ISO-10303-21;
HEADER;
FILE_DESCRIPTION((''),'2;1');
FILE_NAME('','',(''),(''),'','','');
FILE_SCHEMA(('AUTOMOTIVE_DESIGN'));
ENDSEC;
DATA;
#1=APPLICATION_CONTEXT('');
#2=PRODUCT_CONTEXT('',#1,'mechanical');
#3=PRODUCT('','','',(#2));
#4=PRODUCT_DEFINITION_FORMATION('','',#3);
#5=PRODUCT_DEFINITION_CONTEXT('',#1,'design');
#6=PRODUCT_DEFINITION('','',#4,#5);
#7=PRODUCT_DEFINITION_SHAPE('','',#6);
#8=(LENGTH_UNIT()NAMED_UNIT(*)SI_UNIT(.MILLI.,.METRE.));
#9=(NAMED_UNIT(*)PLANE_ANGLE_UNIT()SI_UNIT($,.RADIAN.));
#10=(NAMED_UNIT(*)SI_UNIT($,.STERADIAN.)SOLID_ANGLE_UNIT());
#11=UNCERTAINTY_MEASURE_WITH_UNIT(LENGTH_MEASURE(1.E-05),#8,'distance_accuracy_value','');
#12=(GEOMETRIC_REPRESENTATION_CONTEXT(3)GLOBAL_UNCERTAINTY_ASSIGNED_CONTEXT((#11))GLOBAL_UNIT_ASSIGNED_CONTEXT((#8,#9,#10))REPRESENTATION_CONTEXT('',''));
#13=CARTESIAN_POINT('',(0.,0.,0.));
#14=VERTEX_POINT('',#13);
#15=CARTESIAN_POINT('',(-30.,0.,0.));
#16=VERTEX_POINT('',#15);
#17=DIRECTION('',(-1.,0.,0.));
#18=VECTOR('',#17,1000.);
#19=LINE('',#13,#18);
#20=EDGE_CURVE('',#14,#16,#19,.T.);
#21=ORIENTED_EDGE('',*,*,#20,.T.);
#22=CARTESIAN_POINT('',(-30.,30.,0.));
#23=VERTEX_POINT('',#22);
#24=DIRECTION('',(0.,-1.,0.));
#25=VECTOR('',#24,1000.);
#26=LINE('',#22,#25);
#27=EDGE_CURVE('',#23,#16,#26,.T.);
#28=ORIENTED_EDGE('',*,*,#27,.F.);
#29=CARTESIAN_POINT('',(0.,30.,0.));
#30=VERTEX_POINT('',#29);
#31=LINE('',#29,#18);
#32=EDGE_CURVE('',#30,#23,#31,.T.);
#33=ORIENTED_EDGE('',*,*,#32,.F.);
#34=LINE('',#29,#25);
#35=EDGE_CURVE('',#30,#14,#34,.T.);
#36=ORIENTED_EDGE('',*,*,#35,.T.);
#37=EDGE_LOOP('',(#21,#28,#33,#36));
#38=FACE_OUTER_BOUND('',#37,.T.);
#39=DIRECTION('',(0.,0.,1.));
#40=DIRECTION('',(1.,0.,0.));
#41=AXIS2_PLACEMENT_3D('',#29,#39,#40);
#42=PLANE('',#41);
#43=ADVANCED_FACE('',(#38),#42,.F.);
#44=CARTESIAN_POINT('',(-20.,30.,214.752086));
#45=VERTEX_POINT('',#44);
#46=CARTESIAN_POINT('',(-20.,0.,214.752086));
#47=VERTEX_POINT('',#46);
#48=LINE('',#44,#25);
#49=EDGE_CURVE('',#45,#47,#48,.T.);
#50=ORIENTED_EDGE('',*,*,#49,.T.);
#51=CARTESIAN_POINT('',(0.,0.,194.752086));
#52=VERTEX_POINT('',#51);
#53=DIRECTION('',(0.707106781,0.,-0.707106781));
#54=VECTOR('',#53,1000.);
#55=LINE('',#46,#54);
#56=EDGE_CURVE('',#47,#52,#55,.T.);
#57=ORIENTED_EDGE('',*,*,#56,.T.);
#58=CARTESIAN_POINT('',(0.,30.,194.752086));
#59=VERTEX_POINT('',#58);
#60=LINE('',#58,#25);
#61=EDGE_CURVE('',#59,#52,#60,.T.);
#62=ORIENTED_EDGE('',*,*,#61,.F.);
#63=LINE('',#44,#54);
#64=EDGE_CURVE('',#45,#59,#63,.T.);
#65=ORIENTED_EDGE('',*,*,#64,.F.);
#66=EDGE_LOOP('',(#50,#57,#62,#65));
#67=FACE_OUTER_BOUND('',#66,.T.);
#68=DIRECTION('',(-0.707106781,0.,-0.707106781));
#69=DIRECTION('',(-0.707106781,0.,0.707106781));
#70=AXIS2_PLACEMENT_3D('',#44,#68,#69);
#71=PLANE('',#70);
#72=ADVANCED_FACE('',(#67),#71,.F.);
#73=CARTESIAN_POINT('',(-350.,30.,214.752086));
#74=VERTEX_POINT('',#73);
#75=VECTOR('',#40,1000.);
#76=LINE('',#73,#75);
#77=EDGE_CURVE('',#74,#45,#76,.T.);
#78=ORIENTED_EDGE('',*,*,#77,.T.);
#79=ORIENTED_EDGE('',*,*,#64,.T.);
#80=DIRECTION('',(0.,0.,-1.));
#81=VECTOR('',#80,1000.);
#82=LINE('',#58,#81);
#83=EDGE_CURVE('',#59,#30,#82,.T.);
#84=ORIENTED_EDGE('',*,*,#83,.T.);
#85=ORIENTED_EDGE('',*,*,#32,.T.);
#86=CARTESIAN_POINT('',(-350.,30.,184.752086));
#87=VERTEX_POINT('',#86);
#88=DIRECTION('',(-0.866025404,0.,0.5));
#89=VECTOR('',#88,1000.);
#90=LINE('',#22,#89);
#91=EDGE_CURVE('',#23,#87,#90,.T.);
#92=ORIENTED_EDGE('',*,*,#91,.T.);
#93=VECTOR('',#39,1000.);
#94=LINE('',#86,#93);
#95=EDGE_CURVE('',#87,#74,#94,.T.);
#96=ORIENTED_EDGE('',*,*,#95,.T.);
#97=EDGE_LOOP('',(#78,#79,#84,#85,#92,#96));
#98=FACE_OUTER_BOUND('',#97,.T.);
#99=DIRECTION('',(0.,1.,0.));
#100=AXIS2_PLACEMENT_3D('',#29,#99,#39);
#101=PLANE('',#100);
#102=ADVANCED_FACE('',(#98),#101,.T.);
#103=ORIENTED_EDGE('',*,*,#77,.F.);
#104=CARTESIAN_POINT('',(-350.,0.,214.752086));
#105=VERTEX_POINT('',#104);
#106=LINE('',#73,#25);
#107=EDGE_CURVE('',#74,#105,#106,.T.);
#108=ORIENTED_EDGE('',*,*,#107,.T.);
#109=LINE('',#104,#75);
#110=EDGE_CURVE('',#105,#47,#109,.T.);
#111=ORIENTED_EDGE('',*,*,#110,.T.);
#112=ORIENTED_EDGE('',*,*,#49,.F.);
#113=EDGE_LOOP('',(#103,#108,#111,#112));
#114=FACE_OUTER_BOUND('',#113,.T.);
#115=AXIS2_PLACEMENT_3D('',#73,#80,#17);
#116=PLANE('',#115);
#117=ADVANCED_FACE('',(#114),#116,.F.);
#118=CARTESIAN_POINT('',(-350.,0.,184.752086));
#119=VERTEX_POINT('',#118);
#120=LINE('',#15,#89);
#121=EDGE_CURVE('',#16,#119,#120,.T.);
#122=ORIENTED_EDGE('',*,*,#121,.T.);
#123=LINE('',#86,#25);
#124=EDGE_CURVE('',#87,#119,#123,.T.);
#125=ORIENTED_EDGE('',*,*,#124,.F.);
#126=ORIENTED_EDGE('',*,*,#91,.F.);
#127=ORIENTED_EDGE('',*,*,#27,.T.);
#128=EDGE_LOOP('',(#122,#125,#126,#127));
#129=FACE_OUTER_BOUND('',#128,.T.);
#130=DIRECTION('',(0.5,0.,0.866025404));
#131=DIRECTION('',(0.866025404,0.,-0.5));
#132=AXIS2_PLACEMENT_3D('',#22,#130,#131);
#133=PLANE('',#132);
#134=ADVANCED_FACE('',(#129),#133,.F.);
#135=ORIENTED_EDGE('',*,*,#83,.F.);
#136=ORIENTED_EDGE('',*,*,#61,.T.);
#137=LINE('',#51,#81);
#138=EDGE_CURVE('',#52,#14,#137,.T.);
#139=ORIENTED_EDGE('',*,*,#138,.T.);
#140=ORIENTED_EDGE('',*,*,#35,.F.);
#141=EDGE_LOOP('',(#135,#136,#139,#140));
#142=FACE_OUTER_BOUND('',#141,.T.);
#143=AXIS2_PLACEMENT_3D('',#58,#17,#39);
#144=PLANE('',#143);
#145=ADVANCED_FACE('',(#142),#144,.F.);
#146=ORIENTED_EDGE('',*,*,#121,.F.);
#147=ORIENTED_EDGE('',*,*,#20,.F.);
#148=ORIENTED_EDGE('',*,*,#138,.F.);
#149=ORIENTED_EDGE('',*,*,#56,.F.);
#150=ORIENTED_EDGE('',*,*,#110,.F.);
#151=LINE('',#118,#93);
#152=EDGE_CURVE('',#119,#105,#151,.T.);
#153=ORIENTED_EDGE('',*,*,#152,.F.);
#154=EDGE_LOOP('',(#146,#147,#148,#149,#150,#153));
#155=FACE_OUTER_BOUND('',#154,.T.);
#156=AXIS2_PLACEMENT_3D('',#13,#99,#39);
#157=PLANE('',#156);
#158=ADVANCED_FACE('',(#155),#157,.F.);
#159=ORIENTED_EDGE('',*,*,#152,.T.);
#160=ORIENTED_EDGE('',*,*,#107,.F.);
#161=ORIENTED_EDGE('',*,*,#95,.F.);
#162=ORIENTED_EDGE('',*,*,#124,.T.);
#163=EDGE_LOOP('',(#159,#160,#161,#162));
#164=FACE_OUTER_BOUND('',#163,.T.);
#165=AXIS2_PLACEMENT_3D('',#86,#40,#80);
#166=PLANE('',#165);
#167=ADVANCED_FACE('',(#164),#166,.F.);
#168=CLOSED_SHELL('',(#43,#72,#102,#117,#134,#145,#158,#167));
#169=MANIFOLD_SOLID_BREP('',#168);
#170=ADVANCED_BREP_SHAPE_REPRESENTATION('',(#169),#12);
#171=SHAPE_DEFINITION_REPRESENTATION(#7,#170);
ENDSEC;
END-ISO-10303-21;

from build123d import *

# Parameters (mm, degrees)
EXTRUDE_1_DEPTH = 30


with BuildPart() as part:
    # 草图1 → 凸台-拉伸1 (new body)
    with BuildSketch(Plane(origin=(0, 0, 0), x_dir=(1, 0, 0), z_dir=(0, 1, 0))):
        Polygon((0, 0), (-30, 0), (-350, -184.752086141), (-350, -214.752086141), (-20, -214.752086141), (0, -194.752086141), align=None)
    extrude(amount=EXTRUDE_1_DEPTH)


solid = part.part
